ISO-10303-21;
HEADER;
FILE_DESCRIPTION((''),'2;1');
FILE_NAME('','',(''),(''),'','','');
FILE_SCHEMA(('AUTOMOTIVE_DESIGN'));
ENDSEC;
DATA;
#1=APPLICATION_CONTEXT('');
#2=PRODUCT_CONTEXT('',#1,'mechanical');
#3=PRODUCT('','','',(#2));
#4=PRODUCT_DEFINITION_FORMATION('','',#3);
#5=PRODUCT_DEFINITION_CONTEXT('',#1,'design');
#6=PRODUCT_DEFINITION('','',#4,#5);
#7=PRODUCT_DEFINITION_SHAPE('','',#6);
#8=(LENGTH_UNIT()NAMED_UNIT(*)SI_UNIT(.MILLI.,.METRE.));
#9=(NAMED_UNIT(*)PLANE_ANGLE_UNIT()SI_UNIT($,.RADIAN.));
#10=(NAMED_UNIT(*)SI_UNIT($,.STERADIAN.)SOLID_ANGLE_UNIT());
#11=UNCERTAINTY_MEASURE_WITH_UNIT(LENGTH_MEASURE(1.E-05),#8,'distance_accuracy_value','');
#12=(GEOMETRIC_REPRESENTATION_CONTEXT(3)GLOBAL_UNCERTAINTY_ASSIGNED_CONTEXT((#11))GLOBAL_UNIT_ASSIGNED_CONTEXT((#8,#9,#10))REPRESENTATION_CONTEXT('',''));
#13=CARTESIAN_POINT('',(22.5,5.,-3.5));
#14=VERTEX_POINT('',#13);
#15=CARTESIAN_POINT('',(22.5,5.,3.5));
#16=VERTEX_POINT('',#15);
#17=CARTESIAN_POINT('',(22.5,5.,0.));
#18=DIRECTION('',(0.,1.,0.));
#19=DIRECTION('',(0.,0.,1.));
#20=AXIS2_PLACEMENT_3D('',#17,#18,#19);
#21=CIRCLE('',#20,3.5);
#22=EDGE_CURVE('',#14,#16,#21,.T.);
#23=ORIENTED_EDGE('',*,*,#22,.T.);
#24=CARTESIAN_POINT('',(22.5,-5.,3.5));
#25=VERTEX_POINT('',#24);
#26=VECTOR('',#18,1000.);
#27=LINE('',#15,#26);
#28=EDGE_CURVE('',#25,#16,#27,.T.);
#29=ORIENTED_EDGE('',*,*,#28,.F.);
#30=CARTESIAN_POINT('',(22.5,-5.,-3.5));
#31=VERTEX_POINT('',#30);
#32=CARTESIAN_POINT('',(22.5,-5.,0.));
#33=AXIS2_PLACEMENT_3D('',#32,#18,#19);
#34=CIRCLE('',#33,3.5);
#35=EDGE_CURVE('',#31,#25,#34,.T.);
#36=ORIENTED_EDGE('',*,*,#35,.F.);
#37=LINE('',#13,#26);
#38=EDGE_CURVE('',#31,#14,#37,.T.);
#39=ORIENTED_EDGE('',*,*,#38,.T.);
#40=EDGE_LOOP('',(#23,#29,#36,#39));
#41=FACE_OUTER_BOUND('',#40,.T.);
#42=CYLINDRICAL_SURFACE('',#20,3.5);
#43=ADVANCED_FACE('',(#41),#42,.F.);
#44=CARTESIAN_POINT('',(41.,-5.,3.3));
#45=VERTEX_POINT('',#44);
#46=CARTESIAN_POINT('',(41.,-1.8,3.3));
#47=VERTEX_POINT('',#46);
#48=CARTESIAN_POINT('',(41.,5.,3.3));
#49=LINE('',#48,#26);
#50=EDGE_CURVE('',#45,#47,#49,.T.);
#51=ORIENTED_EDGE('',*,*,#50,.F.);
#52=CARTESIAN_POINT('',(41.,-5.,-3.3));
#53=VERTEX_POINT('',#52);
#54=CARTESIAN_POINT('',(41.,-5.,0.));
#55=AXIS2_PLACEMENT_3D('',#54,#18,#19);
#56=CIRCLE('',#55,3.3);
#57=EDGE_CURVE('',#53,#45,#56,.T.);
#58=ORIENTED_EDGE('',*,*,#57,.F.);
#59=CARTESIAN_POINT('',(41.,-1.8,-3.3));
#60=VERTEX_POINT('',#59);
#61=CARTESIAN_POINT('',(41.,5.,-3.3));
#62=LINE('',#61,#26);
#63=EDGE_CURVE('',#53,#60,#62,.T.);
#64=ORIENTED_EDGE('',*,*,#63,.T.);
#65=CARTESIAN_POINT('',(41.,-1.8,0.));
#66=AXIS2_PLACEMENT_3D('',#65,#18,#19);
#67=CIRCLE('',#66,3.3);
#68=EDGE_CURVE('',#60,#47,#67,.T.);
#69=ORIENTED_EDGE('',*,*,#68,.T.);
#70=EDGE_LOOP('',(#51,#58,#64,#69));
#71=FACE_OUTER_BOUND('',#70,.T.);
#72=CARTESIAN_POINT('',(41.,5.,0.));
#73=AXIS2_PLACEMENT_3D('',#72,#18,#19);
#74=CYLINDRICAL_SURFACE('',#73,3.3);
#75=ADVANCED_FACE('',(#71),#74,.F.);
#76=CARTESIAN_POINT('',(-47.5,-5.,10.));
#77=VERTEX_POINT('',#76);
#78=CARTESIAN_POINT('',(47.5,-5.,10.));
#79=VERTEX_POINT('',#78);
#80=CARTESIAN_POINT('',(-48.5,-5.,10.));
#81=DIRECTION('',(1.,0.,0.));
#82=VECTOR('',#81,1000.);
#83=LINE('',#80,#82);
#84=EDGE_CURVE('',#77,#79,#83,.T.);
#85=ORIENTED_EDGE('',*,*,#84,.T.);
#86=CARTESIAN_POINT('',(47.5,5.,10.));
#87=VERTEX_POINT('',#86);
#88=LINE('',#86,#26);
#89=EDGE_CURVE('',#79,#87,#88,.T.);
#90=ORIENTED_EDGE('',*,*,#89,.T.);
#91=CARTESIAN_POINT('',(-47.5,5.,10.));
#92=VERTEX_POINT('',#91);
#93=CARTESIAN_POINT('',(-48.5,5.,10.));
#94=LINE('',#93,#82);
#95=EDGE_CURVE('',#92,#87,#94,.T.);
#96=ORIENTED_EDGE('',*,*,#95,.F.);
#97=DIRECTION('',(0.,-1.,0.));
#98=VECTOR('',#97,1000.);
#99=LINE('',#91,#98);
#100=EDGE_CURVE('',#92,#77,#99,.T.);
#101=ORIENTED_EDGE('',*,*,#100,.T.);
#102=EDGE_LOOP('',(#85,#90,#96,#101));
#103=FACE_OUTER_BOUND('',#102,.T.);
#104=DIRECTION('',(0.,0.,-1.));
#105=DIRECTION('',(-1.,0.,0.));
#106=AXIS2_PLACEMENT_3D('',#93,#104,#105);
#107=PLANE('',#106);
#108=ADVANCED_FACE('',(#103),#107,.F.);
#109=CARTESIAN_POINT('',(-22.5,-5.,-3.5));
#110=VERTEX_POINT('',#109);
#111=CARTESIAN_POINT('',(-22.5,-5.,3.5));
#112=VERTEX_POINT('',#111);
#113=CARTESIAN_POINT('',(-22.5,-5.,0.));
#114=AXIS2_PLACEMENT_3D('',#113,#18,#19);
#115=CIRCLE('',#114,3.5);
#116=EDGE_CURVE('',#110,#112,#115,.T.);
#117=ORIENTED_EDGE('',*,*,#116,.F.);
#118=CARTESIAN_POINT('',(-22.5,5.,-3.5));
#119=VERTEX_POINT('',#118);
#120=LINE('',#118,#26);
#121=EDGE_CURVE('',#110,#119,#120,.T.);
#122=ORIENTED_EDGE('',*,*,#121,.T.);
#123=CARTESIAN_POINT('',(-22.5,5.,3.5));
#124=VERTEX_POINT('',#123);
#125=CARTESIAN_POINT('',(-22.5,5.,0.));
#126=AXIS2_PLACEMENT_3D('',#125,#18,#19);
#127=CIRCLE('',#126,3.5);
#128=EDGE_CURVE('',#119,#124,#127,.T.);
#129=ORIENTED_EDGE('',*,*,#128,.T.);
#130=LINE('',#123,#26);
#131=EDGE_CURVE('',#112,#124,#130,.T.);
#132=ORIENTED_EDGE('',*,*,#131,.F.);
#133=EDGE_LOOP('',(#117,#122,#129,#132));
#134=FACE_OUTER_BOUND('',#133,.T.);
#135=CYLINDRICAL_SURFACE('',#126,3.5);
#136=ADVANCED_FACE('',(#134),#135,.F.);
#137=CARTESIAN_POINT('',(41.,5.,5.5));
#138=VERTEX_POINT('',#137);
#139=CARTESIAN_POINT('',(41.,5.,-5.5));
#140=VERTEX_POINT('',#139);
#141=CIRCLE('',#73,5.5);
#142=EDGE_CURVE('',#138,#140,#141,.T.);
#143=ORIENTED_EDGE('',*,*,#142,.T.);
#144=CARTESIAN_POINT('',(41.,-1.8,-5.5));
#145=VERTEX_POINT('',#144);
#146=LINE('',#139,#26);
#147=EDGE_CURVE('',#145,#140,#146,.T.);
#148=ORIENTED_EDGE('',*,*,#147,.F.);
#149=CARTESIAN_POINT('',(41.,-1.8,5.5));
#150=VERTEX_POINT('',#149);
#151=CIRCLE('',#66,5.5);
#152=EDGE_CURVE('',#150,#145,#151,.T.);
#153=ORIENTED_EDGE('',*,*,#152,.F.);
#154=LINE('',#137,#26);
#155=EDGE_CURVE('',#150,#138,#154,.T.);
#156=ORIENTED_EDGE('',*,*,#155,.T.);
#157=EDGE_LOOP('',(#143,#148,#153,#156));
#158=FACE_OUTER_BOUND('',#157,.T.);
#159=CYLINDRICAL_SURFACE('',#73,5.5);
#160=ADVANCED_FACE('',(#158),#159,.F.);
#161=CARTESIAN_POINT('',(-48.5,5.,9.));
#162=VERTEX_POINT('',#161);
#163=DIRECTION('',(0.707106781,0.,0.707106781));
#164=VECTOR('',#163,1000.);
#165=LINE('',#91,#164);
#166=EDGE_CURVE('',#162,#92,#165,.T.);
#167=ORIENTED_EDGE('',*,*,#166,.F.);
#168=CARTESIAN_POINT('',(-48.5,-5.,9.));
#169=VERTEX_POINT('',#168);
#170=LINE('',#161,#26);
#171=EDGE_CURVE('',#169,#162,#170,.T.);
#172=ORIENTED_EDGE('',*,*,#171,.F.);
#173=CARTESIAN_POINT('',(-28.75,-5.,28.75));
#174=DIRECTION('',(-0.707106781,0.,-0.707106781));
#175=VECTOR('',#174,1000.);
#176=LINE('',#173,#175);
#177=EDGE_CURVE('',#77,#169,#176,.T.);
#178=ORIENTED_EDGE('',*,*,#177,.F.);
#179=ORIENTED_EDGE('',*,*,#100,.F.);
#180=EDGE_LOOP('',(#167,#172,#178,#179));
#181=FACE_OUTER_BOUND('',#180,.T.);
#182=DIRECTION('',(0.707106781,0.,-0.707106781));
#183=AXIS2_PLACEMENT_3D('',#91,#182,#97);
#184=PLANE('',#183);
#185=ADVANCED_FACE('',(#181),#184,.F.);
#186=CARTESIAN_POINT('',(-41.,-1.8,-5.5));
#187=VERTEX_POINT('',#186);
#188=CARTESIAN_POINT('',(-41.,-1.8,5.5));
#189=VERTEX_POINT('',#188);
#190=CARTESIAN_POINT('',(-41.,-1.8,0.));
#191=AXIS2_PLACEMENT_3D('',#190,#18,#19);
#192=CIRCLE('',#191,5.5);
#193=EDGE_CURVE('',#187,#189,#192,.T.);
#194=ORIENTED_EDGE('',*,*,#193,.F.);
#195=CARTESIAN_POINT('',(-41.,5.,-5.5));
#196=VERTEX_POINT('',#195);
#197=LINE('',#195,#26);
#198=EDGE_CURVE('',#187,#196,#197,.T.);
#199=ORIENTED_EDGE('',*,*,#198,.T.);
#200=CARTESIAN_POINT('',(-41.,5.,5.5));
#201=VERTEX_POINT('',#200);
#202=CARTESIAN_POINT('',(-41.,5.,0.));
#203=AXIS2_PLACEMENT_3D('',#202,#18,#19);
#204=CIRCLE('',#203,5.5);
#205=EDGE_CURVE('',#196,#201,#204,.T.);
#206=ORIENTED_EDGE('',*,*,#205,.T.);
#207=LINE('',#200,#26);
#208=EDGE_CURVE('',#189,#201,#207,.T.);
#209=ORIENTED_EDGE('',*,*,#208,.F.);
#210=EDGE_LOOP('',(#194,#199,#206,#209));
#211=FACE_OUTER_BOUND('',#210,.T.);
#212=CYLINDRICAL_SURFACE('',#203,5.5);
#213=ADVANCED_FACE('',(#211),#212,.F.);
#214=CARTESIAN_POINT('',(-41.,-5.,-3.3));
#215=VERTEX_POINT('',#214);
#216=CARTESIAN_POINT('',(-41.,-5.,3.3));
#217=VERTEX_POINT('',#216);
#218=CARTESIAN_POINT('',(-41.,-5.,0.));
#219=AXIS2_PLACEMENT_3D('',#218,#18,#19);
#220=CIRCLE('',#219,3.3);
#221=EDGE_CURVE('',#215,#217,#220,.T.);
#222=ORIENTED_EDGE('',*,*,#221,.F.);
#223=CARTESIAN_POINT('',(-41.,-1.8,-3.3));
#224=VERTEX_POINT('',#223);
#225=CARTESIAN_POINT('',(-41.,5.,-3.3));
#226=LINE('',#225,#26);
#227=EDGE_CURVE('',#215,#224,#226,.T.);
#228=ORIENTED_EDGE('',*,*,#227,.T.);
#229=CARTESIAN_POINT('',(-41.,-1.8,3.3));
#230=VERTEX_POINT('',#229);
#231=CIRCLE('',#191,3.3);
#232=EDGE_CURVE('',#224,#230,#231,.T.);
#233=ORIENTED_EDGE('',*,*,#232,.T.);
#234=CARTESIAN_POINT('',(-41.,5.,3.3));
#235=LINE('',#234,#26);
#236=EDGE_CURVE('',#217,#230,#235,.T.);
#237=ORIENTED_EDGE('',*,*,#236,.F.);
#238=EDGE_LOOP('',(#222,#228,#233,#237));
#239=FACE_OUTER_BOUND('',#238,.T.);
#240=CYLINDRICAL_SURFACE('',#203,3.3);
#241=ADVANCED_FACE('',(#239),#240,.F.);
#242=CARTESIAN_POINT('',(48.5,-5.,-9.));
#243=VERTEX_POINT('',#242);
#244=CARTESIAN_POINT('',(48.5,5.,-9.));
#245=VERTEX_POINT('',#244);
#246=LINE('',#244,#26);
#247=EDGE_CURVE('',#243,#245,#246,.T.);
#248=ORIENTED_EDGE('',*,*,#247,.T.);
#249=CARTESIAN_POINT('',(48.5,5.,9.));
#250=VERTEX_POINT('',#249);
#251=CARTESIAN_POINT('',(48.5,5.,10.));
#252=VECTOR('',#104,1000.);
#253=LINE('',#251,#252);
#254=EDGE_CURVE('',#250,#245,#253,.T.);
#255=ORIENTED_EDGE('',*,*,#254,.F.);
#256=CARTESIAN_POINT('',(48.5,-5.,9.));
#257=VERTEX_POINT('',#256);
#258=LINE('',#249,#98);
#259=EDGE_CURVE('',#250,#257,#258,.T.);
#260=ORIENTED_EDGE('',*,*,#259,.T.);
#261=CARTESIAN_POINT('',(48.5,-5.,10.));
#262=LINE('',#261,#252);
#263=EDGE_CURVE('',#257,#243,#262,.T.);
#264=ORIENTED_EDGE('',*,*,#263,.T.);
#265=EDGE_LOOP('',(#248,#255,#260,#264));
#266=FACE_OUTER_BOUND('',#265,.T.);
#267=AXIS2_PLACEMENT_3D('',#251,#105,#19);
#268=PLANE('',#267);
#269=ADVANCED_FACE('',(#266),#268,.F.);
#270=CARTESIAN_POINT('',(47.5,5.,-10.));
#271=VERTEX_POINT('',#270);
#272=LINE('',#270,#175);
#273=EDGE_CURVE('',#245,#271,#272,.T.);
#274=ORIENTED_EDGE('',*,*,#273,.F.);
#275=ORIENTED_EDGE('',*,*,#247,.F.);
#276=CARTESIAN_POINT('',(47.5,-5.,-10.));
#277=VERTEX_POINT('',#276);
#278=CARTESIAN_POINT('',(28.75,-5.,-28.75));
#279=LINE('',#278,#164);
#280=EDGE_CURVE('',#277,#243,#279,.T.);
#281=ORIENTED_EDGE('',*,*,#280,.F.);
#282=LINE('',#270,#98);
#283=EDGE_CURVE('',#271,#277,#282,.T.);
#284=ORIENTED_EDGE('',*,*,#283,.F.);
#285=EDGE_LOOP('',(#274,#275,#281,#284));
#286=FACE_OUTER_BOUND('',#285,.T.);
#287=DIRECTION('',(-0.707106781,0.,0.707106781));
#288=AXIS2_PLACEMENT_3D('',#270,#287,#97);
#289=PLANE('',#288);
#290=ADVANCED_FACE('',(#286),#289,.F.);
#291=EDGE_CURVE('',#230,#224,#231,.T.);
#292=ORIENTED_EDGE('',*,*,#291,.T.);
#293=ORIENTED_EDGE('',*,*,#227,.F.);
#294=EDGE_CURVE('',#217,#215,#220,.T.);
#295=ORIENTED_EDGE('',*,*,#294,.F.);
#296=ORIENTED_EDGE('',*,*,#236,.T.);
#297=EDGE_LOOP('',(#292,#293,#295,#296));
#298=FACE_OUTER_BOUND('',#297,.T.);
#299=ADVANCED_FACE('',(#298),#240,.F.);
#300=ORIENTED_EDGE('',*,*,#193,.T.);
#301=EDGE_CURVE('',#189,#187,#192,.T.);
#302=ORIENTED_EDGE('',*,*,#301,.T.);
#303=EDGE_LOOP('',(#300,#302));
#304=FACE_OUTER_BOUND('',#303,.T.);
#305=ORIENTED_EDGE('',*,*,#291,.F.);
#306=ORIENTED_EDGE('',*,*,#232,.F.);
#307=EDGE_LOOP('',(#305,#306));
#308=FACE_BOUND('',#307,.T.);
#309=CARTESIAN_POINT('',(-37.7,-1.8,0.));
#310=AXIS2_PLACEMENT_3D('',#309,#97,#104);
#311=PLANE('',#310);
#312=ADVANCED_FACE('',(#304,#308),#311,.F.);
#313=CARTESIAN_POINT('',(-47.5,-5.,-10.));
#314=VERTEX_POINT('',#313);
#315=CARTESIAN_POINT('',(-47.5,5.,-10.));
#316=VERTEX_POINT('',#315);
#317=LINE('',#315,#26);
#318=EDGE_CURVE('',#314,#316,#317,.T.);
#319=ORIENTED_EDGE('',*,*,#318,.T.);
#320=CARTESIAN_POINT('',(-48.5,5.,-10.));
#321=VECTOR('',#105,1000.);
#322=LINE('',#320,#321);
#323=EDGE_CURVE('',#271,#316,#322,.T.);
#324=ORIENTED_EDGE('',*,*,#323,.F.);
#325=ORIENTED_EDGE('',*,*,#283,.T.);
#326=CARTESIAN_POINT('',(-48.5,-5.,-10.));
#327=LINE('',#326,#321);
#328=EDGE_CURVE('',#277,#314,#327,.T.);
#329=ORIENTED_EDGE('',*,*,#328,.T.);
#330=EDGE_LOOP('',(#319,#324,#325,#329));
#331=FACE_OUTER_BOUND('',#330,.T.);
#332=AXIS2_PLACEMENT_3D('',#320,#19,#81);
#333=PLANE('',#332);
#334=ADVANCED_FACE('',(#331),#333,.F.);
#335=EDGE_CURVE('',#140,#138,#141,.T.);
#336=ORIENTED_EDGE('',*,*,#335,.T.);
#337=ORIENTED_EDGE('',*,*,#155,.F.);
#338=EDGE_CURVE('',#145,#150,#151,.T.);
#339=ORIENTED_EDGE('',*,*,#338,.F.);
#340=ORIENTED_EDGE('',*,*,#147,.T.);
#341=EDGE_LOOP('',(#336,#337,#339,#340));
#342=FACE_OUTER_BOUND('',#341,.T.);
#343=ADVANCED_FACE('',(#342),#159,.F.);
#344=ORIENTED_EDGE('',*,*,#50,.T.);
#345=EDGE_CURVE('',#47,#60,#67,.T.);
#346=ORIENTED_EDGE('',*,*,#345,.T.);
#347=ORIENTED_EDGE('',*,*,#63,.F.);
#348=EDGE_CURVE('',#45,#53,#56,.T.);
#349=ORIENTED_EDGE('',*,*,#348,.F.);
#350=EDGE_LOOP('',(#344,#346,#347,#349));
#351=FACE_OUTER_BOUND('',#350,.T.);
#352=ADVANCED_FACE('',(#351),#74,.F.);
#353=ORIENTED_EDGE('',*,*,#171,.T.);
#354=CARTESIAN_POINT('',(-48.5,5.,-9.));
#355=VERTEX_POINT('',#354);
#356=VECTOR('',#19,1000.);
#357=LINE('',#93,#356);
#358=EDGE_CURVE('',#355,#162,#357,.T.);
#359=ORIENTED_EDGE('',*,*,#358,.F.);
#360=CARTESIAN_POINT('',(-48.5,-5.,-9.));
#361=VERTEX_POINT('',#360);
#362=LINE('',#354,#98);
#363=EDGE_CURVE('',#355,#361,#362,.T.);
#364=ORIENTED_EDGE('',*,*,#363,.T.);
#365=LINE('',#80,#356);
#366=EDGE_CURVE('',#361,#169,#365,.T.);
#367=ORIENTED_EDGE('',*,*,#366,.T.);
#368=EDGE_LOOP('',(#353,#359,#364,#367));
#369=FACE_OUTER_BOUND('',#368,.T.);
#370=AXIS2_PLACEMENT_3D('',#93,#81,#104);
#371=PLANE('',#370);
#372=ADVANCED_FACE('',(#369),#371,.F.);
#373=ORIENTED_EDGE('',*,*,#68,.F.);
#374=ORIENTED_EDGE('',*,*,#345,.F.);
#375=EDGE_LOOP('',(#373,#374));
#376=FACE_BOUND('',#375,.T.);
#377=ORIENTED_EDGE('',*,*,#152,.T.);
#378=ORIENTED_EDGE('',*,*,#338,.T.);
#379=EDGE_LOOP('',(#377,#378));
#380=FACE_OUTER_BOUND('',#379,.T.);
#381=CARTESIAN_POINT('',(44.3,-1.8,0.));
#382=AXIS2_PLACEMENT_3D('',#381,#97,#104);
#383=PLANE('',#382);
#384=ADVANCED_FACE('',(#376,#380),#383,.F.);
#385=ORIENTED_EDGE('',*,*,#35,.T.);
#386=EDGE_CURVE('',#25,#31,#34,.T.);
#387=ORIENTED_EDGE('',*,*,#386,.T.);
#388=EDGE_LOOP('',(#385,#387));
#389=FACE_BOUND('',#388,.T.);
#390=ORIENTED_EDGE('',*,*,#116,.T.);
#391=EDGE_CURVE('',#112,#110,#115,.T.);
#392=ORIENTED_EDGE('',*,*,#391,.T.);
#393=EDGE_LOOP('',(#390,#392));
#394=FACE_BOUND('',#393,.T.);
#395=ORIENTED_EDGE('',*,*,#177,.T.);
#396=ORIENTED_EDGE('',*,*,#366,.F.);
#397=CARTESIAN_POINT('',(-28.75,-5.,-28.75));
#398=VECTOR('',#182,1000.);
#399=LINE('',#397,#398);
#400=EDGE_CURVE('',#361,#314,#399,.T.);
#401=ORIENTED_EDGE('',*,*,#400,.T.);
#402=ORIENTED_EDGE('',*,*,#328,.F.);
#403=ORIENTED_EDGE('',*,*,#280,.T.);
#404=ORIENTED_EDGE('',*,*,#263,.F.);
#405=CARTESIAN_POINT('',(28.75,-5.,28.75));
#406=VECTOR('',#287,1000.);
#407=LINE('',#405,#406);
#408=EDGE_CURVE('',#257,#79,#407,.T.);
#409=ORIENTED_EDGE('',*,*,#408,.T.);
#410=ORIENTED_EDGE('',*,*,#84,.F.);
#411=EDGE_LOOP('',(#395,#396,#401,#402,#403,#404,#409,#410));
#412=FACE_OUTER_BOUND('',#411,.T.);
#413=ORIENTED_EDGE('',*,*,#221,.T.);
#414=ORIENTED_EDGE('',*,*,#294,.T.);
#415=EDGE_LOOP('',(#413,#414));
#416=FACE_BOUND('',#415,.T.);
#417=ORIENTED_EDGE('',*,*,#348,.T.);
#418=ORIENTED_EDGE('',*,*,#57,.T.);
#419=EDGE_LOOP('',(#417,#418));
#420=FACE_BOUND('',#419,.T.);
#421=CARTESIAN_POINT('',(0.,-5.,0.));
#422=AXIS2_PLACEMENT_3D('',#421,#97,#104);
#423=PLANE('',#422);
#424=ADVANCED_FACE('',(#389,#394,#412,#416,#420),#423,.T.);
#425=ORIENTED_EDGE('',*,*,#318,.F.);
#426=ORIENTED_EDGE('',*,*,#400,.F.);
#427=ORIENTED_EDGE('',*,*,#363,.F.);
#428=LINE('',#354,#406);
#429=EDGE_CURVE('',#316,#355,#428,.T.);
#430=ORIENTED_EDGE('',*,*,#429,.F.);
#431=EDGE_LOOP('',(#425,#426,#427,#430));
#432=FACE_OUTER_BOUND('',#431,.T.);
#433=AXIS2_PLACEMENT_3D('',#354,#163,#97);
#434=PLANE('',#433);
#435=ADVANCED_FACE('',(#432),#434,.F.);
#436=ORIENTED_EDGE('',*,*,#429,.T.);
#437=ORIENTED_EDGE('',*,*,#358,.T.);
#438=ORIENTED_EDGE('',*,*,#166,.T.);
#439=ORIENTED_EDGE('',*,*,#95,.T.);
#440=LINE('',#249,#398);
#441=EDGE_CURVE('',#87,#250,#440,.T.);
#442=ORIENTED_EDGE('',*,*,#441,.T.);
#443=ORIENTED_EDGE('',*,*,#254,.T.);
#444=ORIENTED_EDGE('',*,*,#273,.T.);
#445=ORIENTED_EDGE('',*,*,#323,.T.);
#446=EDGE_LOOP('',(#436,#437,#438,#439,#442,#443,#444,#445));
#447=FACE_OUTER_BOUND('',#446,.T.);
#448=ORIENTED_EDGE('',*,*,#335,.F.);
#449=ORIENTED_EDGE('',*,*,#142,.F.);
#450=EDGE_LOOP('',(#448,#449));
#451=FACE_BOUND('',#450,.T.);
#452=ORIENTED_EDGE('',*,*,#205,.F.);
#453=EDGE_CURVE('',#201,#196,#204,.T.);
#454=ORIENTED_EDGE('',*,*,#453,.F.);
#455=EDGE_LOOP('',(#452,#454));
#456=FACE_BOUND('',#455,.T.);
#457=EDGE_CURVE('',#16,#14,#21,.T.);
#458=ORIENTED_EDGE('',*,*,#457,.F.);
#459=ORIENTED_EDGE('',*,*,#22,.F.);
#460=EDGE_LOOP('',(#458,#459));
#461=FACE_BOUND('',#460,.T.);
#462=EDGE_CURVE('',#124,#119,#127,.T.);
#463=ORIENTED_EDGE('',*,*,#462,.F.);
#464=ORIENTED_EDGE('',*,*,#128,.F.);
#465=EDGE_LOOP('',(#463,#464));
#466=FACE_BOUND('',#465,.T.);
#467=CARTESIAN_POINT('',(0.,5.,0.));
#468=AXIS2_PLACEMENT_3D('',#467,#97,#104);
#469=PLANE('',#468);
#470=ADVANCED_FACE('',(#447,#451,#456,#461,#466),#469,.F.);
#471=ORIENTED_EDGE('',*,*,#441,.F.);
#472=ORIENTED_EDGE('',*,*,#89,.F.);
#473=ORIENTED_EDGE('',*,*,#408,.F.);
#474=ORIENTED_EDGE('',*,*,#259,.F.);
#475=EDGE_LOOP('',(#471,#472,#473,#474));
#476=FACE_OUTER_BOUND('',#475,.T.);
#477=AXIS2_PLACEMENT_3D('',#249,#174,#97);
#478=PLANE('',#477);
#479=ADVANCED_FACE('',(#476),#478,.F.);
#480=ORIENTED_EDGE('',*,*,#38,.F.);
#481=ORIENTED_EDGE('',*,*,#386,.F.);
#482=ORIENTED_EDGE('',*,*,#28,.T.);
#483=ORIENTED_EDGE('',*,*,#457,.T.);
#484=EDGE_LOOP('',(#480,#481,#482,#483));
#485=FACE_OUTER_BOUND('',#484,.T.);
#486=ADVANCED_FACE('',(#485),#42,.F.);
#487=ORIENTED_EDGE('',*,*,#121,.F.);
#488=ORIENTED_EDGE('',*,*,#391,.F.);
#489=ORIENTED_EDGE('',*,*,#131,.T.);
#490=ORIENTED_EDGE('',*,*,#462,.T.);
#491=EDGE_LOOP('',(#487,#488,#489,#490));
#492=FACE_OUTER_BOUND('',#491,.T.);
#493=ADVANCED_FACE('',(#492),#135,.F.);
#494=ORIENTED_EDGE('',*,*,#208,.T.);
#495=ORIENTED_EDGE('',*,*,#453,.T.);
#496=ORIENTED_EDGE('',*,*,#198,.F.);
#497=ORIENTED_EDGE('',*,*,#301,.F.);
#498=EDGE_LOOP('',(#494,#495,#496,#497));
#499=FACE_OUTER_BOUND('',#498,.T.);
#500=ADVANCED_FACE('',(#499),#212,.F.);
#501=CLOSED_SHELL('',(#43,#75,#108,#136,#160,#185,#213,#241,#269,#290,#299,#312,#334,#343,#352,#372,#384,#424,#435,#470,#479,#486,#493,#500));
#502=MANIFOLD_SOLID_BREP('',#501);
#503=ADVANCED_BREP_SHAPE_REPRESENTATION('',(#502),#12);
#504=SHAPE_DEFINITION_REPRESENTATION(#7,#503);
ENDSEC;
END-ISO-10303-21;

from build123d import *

# Parameters (mm, degrees)
SKETCH_1_W                   = 97
SKETCH_1_H                   = 20
EXTRUDE_1_DEPTH              = 5
M8X1_0_1_D                   = 7
HOLE_WIZARD_M6_1_D           = 6.6
HOLE_WIZARD_M6_1_CBORE_D     = 11
HOLE_WIZARD_M6_1_CBORE_DEPTH = 6.8
CHAMFER_1_SIZE               = 1


with BuildPart() as part:
    # 草图1 → 凸台-拉伸1 (new, symmetric)
    with BuildSketch(Plane(origin=(0, 0, 0), x_dir=(1, 0, 0), z_dir=(0, 1, 0))):
        Rectangle(SKETCH_1_W, SKETCH_1_H)
    extrude(amount=EXTRUDE_1_DEPTH, both=True)

    # M8x1.0 螺纹孔1 (through all)
    with Locations(Plane(origin=(0, 5, 0), x_dir=(1, 0, 0), z_dir=(0, 1, 0))):
        with Locations((-22.5, 0), (22.5, 0)):
            Hole(M8X1_0_1_D / 2)

    # M6 六角圆柱头螺钉的柱形沉头孔1 (through all)
    with Locations(Plane(origin=(0, 5, -3), x_dir=(-1, 0, 0), z_dir=(0, 1, 0))):
        with Locations((41, 3), (-41, 3)):
            CounterBoreHole(HOLE_WIZARD_M6_1_D / 2, HOLE_WIZARD_M6_1_CBORE_D / 2, HOLE_WIZARD_M6_1_CBORE_DEPTH)

    # 倒角1
    chamfer_1_edges = [part.edges().sort_by_distance(p)[0] for p in [
        (48.5, 0, 10),
        (-48.5, 0, 10),
        (-48.5, 0, -10),
        (48.5, 0, -10),
    ]]
    chamfer(chamfer_1_edges, length=CHAMFER_1_SIZE)


solid = part.part
